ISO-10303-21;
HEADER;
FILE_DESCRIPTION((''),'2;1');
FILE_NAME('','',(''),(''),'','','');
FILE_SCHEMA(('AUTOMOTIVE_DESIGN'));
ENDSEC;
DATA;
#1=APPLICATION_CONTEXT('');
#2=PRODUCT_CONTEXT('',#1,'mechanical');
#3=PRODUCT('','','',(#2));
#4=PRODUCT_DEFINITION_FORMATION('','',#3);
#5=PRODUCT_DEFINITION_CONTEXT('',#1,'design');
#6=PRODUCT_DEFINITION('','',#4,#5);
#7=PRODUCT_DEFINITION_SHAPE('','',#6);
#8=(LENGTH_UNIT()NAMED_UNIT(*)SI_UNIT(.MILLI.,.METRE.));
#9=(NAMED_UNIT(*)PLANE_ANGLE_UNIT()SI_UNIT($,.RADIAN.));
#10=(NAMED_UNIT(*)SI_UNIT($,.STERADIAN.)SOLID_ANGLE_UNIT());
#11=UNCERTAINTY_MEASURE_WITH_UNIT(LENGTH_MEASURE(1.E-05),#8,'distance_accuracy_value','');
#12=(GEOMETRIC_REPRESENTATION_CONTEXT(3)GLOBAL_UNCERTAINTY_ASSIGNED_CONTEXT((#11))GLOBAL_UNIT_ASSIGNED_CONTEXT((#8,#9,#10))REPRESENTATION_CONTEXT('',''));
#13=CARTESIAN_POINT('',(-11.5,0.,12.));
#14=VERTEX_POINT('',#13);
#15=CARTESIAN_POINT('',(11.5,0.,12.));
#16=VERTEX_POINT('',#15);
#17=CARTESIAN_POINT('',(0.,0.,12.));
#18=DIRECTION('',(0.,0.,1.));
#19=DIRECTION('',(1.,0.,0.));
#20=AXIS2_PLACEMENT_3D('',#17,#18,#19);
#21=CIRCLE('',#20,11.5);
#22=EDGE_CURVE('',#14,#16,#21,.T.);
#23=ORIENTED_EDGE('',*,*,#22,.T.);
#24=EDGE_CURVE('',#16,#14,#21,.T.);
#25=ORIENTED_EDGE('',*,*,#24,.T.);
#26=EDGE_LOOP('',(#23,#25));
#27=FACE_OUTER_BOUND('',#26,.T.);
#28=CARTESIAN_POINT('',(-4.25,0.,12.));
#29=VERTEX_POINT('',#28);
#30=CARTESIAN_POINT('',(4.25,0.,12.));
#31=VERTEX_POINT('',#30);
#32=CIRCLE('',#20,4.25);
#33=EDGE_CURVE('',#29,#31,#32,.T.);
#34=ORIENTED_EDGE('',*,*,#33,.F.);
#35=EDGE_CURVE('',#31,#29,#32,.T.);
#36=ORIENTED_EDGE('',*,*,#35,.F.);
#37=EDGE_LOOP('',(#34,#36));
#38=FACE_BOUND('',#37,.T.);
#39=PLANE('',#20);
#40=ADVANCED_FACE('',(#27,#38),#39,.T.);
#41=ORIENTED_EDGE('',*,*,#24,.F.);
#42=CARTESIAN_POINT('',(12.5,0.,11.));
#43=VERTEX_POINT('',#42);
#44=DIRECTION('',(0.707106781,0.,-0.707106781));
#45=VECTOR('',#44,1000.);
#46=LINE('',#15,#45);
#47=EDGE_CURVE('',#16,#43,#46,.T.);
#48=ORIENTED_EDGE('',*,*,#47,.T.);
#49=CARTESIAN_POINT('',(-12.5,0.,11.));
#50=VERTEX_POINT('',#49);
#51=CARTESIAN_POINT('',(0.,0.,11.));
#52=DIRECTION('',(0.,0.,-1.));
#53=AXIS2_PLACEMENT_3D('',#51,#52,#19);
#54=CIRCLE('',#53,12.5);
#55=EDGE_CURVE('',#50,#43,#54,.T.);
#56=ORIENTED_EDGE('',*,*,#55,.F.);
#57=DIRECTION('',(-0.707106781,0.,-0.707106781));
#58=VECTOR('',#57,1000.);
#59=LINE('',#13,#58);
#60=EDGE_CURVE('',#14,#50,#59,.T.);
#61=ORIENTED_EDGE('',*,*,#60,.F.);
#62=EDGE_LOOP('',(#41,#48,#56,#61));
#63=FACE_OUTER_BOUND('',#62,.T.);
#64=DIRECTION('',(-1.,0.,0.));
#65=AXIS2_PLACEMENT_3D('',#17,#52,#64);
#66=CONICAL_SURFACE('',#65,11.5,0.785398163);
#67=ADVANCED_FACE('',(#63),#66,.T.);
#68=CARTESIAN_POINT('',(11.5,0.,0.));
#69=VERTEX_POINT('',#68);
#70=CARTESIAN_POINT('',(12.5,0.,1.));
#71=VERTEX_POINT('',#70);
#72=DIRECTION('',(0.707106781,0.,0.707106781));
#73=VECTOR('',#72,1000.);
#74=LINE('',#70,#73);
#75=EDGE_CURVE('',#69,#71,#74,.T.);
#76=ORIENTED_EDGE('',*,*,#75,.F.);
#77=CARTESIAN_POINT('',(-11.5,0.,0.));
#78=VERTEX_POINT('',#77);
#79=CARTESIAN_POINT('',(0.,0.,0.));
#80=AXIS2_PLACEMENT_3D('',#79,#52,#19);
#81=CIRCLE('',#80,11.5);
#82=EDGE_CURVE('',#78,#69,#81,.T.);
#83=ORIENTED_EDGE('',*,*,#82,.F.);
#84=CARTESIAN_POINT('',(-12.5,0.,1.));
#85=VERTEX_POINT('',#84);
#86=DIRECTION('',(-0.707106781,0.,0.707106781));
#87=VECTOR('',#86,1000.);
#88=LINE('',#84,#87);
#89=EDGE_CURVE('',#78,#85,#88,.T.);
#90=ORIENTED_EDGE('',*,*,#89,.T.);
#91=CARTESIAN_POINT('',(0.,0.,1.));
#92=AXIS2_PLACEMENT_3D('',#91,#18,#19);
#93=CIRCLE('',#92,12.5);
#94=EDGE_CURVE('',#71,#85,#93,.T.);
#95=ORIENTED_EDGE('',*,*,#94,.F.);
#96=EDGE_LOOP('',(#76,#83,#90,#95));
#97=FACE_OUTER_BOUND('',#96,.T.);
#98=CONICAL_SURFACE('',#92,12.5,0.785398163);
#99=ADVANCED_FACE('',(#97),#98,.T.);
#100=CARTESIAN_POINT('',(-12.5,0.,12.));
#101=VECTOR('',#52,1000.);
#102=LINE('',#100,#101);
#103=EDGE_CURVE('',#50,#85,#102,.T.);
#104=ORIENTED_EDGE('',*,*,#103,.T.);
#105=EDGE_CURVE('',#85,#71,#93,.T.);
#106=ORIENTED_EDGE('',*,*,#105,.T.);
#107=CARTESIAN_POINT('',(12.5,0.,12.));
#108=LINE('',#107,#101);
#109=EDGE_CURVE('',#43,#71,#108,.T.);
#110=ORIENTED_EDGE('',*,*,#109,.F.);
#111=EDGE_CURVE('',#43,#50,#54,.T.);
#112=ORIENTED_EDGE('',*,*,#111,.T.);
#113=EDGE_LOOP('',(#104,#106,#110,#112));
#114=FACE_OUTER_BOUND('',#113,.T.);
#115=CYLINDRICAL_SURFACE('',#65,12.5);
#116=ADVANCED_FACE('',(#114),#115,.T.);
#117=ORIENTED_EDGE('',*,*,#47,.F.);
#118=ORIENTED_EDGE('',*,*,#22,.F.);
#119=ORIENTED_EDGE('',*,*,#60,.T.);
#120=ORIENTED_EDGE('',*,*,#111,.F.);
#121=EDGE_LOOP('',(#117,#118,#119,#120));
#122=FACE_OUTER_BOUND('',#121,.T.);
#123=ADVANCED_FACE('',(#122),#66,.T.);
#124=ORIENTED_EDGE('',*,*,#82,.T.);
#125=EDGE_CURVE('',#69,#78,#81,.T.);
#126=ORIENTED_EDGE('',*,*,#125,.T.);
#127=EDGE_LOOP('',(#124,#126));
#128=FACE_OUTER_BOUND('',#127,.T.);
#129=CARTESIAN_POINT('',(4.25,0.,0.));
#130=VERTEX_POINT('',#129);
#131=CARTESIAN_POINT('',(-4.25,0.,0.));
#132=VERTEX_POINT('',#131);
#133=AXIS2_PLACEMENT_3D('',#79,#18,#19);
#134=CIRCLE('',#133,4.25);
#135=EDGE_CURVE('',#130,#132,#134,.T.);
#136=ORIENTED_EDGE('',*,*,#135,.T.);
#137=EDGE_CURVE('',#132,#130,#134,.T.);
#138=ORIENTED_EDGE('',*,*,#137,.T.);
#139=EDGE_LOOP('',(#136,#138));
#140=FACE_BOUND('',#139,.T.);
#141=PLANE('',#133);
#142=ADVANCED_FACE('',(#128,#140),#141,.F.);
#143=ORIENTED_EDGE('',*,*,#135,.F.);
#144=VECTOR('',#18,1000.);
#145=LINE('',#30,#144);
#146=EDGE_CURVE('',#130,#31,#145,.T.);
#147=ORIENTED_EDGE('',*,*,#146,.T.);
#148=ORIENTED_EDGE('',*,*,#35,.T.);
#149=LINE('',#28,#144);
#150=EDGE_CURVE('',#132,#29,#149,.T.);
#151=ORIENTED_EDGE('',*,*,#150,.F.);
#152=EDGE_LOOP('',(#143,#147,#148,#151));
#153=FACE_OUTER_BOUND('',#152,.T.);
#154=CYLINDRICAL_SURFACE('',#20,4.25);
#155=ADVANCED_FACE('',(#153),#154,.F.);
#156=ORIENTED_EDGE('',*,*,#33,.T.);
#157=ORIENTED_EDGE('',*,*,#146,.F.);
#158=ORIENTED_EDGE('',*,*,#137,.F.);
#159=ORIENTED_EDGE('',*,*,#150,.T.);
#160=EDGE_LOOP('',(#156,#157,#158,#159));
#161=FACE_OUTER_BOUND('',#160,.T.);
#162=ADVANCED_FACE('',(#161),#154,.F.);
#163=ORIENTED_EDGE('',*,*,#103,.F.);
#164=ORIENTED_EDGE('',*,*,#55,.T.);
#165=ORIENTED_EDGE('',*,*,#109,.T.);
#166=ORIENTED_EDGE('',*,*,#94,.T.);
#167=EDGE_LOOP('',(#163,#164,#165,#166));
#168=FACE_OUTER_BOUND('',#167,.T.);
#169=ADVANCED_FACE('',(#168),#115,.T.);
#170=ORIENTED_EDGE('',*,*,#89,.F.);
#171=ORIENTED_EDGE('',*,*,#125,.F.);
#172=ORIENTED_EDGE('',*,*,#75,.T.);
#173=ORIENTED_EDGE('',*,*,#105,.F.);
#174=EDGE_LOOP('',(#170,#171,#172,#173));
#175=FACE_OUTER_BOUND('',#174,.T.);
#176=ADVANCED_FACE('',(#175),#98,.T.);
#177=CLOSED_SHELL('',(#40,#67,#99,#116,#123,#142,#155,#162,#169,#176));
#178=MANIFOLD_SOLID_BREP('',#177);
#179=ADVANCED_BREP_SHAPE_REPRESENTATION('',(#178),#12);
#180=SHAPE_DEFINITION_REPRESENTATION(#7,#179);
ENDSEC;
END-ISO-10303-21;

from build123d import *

# Parameters (mm, degrees)
SKETCH1_R           = 12.5
BOSS_EXTRUDE1_DEPTH = 12
M10_TAPPED_HOLE1_D  = 8.5
CHAMFER1_SIZE       = 1


with BuildPart() as part:
    # Sketch1 → Boss-Extrude1 (new body)
    with BuildSketch(Plane.XY):
        Circle(SKETCH1_R)
    extrude(amount=BOSS_EXTRUDE1_DEPTH)

    # M10 Tapped Hole1 (through all)
    with Locations(Plane.XY.offset(12)):
        with Locations((0, 0)):
            Hole(M10_TAPPED_HOLE1_D / 2)

    # Chamfer1
    chamfer1_edges = [part.edges().sort_by_distance(p)[0] for p in [
        (-12.5, 0, 0),
        (-12.5, 0, 12),
    ]]
    chamfer(chamfer1_edges, length=CHAMFER1_SIZE)


solid = part.part
